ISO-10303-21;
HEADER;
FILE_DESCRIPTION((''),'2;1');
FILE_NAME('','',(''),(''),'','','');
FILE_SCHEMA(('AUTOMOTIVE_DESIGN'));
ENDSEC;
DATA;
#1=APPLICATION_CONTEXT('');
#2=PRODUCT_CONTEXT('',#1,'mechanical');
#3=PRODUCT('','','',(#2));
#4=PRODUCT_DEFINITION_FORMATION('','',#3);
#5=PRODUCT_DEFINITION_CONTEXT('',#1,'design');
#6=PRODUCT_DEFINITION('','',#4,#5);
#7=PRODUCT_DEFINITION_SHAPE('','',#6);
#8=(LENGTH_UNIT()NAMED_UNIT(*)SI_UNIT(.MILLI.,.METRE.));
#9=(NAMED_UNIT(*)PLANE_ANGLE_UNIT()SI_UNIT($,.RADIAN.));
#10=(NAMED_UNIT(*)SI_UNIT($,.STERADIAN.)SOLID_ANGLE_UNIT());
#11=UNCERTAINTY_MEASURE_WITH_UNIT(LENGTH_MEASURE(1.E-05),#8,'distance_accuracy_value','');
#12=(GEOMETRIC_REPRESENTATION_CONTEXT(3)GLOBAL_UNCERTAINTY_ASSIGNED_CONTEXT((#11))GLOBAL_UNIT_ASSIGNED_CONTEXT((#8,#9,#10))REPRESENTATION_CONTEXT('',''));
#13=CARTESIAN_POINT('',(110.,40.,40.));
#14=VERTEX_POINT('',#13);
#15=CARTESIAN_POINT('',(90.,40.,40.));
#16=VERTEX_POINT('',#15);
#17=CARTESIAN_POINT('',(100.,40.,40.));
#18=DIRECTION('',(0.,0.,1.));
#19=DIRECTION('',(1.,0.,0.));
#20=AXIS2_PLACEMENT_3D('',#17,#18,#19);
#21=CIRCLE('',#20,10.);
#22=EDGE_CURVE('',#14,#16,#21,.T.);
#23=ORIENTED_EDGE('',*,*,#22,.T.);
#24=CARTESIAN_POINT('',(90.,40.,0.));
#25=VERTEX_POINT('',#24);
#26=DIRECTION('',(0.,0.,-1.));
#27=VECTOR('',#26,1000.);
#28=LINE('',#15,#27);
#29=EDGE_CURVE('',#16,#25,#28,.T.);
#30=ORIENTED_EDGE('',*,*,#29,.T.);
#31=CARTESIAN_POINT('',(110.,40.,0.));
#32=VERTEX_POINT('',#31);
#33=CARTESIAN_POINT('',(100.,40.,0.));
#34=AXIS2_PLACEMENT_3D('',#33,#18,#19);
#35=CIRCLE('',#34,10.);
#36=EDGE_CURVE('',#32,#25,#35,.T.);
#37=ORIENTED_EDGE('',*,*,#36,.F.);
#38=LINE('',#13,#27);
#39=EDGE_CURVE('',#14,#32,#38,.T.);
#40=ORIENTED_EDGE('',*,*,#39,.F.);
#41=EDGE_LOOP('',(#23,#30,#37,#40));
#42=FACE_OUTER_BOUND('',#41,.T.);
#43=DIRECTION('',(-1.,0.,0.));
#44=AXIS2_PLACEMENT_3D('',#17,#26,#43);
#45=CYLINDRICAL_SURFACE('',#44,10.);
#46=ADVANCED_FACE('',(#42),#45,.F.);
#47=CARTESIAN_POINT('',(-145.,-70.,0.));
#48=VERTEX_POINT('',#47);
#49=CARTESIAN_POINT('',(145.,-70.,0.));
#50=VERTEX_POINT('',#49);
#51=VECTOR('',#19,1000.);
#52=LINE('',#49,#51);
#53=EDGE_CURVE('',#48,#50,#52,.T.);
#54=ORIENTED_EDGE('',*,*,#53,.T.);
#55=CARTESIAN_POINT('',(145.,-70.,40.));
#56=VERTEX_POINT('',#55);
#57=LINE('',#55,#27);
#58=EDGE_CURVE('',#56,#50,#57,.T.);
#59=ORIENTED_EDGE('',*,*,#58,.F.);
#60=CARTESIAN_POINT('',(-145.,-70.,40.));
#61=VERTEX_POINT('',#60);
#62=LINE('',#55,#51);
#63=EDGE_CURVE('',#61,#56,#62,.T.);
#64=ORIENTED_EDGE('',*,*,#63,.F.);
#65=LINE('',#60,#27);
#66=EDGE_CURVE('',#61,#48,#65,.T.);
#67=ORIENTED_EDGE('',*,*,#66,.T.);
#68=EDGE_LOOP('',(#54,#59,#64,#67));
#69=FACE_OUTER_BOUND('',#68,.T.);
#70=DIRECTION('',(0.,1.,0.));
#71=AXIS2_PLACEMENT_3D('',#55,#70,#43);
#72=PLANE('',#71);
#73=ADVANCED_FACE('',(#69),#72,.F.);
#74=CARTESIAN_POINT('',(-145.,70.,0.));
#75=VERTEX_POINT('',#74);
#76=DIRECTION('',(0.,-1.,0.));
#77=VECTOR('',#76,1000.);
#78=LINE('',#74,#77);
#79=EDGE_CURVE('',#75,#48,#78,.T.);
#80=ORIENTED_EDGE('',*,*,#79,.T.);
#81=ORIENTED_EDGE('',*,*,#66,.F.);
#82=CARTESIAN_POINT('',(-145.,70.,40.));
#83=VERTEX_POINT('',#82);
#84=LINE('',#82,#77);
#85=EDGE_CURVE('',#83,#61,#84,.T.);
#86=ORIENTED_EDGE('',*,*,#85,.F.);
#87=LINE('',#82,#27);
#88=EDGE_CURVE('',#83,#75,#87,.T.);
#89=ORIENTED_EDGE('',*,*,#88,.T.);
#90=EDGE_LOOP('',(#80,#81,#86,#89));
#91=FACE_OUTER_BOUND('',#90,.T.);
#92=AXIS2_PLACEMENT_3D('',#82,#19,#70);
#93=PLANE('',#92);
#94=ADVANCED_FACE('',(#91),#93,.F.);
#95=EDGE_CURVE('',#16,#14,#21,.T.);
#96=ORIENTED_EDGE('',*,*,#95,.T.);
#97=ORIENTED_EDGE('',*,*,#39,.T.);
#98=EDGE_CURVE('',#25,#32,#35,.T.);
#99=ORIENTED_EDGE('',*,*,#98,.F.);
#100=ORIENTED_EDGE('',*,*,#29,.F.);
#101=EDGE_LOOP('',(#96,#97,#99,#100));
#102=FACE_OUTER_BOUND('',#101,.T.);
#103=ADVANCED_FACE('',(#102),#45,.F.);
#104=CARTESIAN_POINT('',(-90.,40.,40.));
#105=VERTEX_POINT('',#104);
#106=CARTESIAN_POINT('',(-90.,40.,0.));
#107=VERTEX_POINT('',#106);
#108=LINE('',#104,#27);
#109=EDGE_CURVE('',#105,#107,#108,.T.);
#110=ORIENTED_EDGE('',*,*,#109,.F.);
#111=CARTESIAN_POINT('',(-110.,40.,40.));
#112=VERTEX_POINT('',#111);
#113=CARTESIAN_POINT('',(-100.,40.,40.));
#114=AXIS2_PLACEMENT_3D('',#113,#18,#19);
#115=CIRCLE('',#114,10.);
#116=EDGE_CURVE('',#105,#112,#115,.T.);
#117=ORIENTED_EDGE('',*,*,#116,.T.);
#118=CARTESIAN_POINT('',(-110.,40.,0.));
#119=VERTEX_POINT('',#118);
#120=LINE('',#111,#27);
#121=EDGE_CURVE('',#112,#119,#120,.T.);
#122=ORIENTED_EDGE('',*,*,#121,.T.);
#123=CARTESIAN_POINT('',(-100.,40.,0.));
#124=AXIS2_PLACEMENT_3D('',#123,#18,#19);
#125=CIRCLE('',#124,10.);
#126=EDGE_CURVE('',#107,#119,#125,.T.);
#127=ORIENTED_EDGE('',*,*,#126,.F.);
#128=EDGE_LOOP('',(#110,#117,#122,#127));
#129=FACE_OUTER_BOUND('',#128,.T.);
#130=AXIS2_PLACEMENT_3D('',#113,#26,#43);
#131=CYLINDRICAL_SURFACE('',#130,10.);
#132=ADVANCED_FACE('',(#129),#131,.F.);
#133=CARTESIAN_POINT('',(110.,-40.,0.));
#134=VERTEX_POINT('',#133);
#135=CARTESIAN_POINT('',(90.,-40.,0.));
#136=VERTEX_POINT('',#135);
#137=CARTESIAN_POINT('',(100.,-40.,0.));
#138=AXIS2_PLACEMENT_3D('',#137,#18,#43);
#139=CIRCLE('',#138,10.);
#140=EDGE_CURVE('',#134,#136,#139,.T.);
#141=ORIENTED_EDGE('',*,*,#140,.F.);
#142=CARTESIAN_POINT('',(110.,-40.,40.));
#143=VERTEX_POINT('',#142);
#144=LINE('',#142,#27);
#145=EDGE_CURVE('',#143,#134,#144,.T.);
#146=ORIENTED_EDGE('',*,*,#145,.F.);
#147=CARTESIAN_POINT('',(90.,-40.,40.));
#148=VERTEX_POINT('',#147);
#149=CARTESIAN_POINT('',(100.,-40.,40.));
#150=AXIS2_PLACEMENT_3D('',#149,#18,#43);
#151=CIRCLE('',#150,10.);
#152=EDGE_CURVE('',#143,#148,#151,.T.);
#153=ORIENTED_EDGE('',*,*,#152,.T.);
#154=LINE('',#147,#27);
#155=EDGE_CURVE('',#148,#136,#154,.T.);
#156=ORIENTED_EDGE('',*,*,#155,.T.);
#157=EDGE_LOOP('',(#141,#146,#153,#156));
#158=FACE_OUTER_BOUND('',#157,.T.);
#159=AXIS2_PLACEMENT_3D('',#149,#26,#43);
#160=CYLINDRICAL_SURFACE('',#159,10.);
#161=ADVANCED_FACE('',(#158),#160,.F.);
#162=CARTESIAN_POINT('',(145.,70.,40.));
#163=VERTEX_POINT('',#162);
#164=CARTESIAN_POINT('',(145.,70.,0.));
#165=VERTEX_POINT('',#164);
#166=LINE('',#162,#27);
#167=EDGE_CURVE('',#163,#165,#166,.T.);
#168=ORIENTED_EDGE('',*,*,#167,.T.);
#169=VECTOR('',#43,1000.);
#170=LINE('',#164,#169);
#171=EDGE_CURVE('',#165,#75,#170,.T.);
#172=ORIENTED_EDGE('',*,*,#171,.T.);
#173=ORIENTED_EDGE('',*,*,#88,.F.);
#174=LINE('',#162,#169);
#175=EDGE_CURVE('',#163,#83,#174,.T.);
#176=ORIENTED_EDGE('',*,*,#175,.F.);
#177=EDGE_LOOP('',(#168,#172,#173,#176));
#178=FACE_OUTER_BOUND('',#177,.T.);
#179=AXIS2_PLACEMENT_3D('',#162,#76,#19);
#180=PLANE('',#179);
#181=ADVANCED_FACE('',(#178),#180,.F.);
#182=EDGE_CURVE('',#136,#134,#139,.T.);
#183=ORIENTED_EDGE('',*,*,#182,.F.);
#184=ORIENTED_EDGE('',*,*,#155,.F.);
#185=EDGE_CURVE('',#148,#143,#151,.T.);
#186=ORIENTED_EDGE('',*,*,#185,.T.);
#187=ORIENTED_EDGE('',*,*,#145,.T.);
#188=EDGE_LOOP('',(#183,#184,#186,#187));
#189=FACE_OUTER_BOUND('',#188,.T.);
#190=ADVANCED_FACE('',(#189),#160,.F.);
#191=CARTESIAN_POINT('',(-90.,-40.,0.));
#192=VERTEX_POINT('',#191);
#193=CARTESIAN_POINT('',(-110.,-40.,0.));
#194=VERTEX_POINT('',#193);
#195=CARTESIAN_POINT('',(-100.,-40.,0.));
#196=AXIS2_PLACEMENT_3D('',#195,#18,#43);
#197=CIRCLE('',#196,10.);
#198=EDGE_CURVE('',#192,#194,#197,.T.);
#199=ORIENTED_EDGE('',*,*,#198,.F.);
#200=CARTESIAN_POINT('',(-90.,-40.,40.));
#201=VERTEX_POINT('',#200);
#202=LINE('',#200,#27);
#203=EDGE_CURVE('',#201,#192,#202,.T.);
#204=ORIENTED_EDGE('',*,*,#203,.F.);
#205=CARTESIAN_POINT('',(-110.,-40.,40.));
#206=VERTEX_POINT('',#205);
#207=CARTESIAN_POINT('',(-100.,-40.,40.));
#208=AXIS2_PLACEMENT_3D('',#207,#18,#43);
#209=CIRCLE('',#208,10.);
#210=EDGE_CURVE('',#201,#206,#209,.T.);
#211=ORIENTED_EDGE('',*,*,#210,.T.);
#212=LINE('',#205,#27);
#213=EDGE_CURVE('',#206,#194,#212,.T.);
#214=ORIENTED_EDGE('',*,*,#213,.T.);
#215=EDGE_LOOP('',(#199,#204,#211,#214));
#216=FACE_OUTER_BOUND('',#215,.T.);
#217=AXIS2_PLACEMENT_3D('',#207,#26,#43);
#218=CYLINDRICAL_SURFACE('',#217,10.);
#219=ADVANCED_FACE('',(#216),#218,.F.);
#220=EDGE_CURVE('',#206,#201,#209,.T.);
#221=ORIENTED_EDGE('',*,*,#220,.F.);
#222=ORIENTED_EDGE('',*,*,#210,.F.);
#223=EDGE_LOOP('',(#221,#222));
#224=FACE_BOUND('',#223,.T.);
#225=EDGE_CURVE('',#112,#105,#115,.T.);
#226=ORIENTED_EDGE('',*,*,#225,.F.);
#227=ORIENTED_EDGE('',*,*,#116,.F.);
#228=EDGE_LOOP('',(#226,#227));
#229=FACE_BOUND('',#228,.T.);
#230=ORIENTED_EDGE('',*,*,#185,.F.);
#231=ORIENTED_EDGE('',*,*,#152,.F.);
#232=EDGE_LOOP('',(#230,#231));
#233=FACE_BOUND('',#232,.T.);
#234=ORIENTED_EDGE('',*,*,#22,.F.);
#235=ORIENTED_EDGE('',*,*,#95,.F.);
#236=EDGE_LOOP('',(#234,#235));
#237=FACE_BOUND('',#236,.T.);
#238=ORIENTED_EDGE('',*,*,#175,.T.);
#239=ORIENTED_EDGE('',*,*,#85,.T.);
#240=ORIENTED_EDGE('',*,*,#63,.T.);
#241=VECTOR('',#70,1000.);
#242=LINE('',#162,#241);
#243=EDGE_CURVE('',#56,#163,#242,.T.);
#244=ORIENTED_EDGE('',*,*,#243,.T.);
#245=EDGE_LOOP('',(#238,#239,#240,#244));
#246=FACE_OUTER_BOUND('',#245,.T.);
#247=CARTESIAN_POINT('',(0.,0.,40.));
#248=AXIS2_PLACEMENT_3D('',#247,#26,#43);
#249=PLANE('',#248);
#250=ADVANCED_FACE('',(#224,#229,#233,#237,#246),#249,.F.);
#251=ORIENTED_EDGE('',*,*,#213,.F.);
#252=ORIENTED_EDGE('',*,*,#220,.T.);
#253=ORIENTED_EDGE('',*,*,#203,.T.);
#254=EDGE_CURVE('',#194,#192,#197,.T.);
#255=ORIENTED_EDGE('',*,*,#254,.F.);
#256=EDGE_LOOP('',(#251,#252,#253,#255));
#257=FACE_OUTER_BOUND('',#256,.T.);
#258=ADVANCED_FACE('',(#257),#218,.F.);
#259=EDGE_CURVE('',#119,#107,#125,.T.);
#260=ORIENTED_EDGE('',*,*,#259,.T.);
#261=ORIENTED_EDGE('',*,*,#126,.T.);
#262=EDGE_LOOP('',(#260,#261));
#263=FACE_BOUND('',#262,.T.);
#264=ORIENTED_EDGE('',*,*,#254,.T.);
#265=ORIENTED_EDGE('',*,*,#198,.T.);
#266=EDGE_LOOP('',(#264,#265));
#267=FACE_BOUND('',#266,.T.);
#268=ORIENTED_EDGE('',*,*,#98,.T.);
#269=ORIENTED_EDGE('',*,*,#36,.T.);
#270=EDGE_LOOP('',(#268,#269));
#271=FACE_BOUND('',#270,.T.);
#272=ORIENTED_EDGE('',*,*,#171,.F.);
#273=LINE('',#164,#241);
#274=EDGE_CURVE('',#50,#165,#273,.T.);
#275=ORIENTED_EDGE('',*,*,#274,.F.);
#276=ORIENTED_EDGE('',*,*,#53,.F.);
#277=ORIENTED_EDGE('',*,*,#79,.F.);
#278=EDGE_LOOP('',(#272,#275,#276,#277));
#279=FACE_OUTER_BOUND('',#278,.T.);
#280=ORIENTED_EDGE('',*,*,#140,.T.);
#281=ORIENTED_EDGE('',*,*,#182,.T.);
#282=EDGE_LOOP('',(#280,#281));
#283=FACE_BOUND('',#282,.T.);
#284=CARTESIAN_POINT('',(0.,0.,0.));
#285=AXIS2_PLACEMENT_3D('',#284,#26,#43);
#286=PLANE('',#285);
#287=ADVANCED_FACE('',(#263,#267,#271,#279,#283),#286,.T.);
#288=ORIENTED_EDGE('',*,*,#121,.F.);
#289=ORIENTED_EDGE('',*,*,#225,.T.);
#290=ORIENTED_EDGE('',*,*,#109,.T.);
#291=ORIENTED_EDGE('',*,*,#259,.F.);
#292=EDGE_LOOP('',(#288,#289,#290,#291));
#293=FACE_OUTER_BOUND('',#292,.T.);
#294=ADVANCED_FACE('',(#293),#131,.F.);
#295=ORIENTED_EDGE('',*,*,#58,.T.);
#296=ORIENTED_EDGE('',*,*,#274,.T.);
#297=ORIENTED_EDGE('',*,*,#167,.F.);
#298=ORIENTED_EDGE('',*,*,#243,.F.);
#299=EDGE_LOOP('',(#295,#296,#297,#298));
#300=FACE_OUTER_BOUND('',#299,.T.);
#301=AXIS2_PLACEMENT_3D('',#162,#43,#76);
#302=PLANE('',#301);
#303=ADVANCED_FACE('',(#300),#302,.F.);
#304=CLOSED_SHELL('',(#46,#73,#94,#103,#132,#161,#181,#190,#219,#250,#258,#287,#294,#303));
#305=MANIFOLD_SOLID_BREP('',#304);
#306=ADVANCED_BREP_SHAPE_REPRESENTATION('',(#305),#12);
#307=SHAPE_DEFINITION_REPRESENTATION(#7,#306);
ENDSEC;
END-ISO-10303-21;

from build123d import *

# Parameters (mm, degrees)
SKETCH1_W           = 290
SKETCH1_H           = 140
SKETCH1_R           = 10
BOSS_EXTRUDE1_DEPTH = 40


with BuildPart() as part:
    # Sketch1 → Boss-Extrude1 (new body)
    with BuildSketch(Plane.XY):
        Rectangle(SKETCH1_W, SKETCH1_H)
        with Locations((-100, 40)):
            Circle(SKETCH1_R, mode=Mode.SUBTRACT)
        with Locations((100, 40)):
            Circle(SKETCH1_R, mode=Mode.SUBTRACT)
        with Locations(Location((100, -40, 0), (0, 0, 180))):
            Circle(SKETCH1_R, mode=Mode.SUBTRACT)
        with Locations(Location((-100, -40, 0), (0, 0, 180))):
            Circle(SKETCH1_R, mode=Mode.SUBTRACT)
    extrude(amount=BOSS_EXTRUDE1_DEPTH)


solid = part.part
